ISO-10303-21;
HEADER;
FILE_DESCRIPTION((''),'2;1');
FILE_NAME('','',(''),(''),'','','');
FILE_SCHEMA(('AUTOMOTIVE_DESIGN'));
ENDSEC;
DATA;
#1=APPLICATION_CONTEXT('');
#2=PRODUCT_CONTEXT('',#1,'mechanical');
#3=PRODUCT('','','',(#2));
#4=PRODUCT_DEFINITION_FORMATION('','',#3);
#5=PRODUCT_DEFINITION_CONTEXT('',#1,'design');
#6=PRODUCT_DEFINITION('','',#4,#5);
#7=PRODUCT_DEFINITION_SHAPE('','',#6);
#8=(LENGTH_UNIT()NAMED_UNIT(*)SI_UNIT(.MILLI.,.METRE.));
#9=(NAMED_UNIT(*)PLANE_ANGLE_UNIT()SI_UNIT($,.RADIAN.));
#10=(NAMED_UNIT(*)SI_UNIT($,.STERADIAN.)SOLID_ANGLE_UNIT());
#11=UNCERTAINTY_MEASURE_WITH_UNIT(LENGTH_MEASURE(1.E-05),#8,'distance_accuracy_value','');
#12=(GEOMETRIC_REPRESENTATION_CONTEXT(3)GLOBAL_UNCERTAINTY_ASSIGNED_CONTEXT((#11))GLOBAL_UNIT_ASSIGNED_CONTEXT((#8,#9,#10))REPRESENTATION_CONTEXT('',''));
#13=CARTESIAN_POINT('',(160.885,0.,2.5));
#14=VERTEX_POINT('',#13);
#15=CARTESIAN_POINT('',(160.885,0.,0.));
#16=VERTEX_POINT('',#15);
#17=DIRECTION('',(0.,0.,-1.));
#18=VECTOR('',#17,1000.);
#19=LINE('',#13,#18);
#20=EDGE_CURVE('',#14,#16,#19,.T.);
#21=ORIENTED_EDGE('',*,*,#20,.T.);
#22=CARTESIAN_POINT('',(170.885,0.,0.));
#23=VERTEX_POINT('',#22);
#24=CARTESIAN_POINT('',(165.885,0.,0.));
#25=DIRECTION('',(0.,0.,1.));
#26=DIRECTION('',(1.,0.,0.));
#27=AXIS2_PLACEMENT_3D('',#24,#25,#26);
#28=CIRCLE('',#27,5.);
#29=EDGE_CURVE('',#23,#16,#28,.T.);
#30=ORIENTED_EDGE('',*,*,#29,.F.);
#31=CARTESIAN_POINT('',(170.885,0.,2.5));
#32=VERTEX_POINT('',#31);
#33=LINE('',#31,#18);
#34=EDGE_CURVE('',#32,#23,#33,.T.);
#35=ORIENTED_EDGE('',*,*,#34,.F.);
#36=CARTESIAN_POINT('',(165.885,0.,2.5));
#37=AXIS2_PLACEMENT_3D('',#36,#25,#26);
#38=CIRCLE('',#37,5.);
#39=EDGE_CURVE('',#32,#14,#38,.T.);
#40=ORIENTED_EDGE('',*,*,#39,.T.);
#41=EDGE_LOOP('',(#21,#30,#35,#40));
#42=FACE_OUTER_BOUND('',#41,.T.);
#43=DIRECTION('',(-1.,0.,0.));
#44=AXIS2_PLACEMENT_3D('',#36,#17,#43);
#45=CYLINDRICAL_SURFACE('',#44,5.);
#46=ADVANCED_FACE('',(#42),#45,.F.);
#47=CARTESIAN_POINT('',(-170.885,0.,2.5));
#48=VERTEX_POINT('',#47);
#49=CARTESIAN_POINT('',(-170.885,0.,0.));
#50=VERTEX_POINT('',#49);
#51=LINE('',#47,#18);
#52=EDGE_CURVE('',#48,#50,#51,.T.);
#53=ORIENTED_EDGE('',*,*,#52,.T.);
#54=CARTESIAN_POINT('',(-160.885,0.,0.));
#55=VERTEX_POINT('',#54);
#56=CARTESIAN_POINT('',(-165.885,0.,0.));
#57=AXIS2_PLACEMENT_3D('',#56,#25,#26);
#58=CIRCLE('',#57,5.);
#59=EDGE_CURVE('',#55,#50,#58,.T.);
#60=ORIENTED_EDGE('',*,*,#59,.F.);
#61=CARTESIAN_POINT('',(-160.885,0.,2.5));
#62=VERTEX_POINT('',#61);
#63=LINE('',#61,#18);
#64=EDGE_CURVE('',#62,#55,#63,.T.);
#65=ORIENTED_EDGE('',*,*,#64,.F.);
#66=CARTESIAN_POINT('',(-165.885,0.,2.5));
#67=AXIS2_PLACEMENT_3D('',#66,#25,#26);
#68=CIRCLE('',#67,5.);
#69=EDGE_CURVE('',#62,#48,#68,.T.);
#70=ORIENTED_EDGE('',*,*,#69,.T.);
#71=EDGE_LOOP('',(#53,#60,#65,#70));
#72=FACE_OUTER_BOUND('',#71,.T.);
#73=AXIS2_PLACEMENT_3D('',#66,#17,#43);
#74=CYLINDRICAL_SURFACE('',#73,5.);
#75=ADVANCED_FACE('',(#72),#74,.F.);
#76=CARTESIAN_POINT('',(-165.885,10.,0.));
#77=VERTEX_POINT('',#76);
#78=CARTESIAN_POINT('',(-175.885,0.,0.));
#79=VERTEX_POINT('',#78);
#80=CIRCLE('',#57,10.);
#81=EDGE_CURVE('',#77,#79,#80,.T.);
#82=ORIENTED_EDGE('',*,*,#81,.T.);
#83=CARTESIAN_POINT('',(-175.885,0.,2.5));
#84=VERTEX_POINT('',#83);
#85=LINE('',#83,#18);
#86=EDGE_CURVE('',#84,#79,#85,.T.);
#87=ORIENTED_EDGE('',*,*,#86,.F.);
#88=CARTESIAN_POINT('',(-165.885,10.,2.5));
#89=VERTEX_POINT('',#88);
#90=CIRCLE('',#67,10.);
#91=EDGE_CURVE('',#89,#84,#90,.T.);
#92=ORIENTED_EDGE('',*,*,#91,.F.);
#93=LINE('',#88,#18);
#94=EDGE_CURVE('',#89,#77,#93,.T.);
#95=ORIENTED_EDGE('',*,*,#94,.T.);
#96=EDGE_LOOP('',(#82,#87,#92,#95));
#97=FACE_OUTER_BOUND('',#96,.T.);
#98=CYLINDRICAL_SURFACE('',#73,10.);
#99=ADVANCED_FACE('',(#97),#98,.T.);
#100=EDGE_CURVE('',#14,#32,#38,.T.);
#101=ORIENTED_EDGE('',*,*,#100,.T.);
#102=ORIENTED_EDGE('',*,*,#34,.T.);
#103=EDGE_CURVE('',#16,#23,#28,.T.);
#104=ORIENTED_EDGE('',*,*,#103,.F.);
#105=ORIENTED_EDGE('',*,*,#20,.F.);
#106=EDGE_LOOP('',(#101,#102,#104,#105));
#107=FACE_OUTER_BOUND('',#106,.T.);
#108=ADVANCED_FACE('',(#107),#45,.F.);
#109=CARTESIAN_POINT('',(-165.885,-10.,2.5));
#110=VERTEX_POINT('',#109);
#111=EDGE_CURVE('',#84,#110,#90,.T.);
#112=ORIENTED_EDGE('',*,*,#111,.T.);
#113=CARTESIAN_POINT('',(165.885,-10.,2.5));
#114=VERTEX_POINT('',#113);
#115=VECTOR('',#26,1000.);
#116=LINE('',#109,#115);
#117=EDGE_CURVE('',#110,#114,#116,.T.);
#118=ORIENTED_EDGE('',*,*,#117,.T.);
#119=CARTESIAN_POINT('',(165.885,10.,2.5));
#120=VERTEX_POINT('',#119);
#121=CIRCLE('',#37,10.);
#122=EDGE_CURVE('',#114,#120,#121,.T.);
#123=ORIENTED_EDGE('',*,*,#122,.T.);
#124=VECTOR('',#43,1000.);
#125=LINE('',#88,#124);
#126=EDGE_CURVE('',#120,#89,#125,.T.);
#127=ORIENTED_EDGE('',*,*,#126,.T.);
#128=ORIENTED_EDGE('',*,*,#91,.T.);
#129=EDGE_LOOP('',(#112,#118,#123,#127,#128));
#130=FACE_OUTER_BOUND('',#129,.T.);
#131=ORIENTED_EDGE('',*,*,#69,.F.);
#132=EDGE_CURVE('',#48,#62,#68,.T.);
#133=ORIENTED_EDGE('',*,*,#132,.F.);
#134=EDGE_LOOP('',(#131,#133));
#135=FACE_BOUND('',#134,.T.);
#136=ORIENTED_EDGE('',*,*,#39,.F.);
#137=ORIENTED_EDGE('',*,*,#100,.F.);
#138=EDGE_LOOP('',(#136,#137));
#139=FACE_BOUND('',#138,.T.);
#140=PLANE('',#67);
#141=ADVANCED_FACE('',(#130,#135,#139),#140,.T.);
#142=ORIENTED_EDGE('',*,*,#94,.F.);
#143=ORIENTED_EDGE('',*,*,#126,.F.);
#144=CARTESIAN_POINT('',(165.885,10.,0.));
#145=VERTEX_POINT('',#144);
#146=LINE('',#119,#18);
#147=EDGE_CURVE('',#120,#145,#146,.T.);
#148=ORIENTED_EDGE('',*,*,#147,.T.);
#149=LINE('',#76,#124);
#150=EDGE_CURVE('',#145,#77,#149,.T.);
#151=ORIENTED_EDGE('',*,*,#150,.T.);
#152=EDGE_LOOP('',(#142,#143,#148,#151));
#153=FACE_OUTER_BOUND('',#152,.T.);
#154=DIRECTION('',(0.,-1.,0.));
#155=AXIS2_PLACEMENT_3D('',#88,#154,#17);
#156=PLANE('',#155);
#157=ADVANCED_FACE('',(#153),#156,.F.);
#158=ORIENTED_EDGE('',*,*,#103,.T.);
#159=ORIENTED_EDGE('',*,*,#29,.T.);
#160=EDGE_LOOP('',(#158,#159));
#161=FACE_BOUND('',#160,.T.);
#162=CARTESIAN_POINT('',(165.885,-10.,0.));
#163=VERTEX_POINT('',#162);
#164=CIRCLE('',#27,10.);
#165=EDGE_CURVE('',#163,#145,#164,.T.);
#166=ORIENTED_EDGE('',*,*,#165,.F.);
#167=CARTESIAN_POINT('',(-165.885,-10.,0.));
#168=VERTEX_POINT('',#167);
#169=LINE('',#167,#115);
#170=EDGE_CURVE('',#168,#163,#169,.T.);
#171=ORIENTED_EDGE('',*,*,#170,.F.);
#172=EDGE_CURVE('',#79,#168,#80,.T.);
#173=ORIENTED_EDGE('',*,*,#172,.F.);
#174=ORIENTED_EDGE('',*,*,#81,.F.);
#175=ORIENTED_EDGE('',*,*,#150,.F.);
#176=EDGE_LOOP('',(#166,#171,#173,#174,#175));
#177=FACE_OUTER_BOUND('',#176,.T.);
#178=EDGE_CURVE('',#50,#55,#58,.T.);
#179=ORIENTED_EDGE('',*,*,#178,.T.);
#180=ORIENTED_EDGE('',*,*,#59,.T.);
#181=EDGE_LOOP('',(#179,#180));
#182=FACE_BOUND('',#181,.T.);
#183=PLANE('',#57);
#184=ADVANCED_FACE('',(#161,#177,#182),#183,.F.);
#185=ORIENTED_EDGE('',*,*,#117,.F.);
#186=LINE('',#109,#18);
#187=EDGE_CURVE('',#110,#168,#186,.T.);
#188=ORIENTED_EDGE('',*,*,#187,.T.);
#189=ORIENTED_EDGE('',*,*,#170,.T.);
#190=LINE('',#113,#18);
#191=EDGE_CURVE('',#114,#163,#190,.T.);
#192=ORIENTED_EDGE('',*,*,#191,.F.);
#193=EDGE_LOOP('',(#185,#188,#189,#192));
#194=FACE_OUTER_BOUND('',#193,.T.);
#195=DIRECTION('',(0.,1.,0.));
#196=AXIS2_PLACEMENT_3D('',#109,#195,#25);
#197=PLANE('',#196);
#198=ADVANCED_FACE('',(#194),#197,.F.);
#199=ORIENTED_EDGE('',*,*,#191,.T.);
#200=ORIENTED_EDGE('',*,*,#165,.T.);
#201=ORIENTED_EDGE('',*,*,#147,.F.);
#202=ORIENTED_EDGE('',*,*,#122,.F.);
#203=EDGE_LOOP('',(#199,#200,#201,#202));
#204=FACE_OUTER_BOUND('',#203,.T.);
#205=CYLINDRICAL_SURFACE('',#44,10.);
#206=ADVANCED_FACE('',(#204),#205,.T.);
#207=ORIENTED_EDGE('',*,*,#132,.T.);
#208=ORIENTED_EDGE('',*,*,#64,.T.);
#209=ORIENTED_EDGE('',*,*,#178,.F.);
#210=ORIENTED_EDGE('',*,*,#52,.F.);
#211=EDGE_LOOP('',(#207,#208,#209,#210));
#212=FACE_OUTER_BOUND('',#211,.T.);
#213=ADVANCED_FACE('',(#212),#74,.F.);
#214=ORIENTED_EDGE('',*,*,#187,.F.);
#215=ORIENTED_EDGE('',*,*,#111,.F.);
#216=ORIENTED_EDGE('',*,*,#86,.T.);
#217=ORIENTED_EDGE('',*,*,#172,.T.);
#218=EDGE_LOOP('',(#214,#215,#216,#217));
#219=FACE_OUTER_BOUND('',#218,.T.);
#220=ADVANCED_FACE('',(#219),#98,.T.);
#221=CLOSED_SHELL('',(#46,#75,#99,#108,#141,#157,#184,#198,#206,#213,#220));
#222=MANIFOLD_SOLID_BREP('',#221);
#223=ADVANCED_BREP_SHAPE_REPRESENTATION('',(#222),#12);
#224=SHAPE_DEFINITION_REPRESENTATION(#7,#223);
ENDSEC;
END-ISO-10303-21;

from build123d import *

# Parameters (mm, degrees)
SKETCH1_R           = 5
BOSS_EXTRUDE1_DEPTH = 2.5


with BuildPart() as part:
    # Sketch1 → Boss-Extrude1 (new body)
    with BuildSketch(Plane.XY):
        with BuildLine():
            Line((-165.885, 10), (165.885, 10))
            ThreePointArc((165.885, 10), (175.885, 0), (165.885, -10))
            Line((165.885, -10), (-165.885, -10))
            ThreePointArc((-165.885, -10), (-175.885, 0), (-165.885, 10))
        make_face()
        with Locations((-165.885, 0)):
            Circle(SKETCH1_R, mode=Mode.SUBTRACT)
        with Locations((165.885, 0)):
            Circle(SKETCH1_R, mode=Mode.SUBTRACT)
    extrude(amount=BOSS_EXTRUDE1_DEPTH)


solid = part.part
